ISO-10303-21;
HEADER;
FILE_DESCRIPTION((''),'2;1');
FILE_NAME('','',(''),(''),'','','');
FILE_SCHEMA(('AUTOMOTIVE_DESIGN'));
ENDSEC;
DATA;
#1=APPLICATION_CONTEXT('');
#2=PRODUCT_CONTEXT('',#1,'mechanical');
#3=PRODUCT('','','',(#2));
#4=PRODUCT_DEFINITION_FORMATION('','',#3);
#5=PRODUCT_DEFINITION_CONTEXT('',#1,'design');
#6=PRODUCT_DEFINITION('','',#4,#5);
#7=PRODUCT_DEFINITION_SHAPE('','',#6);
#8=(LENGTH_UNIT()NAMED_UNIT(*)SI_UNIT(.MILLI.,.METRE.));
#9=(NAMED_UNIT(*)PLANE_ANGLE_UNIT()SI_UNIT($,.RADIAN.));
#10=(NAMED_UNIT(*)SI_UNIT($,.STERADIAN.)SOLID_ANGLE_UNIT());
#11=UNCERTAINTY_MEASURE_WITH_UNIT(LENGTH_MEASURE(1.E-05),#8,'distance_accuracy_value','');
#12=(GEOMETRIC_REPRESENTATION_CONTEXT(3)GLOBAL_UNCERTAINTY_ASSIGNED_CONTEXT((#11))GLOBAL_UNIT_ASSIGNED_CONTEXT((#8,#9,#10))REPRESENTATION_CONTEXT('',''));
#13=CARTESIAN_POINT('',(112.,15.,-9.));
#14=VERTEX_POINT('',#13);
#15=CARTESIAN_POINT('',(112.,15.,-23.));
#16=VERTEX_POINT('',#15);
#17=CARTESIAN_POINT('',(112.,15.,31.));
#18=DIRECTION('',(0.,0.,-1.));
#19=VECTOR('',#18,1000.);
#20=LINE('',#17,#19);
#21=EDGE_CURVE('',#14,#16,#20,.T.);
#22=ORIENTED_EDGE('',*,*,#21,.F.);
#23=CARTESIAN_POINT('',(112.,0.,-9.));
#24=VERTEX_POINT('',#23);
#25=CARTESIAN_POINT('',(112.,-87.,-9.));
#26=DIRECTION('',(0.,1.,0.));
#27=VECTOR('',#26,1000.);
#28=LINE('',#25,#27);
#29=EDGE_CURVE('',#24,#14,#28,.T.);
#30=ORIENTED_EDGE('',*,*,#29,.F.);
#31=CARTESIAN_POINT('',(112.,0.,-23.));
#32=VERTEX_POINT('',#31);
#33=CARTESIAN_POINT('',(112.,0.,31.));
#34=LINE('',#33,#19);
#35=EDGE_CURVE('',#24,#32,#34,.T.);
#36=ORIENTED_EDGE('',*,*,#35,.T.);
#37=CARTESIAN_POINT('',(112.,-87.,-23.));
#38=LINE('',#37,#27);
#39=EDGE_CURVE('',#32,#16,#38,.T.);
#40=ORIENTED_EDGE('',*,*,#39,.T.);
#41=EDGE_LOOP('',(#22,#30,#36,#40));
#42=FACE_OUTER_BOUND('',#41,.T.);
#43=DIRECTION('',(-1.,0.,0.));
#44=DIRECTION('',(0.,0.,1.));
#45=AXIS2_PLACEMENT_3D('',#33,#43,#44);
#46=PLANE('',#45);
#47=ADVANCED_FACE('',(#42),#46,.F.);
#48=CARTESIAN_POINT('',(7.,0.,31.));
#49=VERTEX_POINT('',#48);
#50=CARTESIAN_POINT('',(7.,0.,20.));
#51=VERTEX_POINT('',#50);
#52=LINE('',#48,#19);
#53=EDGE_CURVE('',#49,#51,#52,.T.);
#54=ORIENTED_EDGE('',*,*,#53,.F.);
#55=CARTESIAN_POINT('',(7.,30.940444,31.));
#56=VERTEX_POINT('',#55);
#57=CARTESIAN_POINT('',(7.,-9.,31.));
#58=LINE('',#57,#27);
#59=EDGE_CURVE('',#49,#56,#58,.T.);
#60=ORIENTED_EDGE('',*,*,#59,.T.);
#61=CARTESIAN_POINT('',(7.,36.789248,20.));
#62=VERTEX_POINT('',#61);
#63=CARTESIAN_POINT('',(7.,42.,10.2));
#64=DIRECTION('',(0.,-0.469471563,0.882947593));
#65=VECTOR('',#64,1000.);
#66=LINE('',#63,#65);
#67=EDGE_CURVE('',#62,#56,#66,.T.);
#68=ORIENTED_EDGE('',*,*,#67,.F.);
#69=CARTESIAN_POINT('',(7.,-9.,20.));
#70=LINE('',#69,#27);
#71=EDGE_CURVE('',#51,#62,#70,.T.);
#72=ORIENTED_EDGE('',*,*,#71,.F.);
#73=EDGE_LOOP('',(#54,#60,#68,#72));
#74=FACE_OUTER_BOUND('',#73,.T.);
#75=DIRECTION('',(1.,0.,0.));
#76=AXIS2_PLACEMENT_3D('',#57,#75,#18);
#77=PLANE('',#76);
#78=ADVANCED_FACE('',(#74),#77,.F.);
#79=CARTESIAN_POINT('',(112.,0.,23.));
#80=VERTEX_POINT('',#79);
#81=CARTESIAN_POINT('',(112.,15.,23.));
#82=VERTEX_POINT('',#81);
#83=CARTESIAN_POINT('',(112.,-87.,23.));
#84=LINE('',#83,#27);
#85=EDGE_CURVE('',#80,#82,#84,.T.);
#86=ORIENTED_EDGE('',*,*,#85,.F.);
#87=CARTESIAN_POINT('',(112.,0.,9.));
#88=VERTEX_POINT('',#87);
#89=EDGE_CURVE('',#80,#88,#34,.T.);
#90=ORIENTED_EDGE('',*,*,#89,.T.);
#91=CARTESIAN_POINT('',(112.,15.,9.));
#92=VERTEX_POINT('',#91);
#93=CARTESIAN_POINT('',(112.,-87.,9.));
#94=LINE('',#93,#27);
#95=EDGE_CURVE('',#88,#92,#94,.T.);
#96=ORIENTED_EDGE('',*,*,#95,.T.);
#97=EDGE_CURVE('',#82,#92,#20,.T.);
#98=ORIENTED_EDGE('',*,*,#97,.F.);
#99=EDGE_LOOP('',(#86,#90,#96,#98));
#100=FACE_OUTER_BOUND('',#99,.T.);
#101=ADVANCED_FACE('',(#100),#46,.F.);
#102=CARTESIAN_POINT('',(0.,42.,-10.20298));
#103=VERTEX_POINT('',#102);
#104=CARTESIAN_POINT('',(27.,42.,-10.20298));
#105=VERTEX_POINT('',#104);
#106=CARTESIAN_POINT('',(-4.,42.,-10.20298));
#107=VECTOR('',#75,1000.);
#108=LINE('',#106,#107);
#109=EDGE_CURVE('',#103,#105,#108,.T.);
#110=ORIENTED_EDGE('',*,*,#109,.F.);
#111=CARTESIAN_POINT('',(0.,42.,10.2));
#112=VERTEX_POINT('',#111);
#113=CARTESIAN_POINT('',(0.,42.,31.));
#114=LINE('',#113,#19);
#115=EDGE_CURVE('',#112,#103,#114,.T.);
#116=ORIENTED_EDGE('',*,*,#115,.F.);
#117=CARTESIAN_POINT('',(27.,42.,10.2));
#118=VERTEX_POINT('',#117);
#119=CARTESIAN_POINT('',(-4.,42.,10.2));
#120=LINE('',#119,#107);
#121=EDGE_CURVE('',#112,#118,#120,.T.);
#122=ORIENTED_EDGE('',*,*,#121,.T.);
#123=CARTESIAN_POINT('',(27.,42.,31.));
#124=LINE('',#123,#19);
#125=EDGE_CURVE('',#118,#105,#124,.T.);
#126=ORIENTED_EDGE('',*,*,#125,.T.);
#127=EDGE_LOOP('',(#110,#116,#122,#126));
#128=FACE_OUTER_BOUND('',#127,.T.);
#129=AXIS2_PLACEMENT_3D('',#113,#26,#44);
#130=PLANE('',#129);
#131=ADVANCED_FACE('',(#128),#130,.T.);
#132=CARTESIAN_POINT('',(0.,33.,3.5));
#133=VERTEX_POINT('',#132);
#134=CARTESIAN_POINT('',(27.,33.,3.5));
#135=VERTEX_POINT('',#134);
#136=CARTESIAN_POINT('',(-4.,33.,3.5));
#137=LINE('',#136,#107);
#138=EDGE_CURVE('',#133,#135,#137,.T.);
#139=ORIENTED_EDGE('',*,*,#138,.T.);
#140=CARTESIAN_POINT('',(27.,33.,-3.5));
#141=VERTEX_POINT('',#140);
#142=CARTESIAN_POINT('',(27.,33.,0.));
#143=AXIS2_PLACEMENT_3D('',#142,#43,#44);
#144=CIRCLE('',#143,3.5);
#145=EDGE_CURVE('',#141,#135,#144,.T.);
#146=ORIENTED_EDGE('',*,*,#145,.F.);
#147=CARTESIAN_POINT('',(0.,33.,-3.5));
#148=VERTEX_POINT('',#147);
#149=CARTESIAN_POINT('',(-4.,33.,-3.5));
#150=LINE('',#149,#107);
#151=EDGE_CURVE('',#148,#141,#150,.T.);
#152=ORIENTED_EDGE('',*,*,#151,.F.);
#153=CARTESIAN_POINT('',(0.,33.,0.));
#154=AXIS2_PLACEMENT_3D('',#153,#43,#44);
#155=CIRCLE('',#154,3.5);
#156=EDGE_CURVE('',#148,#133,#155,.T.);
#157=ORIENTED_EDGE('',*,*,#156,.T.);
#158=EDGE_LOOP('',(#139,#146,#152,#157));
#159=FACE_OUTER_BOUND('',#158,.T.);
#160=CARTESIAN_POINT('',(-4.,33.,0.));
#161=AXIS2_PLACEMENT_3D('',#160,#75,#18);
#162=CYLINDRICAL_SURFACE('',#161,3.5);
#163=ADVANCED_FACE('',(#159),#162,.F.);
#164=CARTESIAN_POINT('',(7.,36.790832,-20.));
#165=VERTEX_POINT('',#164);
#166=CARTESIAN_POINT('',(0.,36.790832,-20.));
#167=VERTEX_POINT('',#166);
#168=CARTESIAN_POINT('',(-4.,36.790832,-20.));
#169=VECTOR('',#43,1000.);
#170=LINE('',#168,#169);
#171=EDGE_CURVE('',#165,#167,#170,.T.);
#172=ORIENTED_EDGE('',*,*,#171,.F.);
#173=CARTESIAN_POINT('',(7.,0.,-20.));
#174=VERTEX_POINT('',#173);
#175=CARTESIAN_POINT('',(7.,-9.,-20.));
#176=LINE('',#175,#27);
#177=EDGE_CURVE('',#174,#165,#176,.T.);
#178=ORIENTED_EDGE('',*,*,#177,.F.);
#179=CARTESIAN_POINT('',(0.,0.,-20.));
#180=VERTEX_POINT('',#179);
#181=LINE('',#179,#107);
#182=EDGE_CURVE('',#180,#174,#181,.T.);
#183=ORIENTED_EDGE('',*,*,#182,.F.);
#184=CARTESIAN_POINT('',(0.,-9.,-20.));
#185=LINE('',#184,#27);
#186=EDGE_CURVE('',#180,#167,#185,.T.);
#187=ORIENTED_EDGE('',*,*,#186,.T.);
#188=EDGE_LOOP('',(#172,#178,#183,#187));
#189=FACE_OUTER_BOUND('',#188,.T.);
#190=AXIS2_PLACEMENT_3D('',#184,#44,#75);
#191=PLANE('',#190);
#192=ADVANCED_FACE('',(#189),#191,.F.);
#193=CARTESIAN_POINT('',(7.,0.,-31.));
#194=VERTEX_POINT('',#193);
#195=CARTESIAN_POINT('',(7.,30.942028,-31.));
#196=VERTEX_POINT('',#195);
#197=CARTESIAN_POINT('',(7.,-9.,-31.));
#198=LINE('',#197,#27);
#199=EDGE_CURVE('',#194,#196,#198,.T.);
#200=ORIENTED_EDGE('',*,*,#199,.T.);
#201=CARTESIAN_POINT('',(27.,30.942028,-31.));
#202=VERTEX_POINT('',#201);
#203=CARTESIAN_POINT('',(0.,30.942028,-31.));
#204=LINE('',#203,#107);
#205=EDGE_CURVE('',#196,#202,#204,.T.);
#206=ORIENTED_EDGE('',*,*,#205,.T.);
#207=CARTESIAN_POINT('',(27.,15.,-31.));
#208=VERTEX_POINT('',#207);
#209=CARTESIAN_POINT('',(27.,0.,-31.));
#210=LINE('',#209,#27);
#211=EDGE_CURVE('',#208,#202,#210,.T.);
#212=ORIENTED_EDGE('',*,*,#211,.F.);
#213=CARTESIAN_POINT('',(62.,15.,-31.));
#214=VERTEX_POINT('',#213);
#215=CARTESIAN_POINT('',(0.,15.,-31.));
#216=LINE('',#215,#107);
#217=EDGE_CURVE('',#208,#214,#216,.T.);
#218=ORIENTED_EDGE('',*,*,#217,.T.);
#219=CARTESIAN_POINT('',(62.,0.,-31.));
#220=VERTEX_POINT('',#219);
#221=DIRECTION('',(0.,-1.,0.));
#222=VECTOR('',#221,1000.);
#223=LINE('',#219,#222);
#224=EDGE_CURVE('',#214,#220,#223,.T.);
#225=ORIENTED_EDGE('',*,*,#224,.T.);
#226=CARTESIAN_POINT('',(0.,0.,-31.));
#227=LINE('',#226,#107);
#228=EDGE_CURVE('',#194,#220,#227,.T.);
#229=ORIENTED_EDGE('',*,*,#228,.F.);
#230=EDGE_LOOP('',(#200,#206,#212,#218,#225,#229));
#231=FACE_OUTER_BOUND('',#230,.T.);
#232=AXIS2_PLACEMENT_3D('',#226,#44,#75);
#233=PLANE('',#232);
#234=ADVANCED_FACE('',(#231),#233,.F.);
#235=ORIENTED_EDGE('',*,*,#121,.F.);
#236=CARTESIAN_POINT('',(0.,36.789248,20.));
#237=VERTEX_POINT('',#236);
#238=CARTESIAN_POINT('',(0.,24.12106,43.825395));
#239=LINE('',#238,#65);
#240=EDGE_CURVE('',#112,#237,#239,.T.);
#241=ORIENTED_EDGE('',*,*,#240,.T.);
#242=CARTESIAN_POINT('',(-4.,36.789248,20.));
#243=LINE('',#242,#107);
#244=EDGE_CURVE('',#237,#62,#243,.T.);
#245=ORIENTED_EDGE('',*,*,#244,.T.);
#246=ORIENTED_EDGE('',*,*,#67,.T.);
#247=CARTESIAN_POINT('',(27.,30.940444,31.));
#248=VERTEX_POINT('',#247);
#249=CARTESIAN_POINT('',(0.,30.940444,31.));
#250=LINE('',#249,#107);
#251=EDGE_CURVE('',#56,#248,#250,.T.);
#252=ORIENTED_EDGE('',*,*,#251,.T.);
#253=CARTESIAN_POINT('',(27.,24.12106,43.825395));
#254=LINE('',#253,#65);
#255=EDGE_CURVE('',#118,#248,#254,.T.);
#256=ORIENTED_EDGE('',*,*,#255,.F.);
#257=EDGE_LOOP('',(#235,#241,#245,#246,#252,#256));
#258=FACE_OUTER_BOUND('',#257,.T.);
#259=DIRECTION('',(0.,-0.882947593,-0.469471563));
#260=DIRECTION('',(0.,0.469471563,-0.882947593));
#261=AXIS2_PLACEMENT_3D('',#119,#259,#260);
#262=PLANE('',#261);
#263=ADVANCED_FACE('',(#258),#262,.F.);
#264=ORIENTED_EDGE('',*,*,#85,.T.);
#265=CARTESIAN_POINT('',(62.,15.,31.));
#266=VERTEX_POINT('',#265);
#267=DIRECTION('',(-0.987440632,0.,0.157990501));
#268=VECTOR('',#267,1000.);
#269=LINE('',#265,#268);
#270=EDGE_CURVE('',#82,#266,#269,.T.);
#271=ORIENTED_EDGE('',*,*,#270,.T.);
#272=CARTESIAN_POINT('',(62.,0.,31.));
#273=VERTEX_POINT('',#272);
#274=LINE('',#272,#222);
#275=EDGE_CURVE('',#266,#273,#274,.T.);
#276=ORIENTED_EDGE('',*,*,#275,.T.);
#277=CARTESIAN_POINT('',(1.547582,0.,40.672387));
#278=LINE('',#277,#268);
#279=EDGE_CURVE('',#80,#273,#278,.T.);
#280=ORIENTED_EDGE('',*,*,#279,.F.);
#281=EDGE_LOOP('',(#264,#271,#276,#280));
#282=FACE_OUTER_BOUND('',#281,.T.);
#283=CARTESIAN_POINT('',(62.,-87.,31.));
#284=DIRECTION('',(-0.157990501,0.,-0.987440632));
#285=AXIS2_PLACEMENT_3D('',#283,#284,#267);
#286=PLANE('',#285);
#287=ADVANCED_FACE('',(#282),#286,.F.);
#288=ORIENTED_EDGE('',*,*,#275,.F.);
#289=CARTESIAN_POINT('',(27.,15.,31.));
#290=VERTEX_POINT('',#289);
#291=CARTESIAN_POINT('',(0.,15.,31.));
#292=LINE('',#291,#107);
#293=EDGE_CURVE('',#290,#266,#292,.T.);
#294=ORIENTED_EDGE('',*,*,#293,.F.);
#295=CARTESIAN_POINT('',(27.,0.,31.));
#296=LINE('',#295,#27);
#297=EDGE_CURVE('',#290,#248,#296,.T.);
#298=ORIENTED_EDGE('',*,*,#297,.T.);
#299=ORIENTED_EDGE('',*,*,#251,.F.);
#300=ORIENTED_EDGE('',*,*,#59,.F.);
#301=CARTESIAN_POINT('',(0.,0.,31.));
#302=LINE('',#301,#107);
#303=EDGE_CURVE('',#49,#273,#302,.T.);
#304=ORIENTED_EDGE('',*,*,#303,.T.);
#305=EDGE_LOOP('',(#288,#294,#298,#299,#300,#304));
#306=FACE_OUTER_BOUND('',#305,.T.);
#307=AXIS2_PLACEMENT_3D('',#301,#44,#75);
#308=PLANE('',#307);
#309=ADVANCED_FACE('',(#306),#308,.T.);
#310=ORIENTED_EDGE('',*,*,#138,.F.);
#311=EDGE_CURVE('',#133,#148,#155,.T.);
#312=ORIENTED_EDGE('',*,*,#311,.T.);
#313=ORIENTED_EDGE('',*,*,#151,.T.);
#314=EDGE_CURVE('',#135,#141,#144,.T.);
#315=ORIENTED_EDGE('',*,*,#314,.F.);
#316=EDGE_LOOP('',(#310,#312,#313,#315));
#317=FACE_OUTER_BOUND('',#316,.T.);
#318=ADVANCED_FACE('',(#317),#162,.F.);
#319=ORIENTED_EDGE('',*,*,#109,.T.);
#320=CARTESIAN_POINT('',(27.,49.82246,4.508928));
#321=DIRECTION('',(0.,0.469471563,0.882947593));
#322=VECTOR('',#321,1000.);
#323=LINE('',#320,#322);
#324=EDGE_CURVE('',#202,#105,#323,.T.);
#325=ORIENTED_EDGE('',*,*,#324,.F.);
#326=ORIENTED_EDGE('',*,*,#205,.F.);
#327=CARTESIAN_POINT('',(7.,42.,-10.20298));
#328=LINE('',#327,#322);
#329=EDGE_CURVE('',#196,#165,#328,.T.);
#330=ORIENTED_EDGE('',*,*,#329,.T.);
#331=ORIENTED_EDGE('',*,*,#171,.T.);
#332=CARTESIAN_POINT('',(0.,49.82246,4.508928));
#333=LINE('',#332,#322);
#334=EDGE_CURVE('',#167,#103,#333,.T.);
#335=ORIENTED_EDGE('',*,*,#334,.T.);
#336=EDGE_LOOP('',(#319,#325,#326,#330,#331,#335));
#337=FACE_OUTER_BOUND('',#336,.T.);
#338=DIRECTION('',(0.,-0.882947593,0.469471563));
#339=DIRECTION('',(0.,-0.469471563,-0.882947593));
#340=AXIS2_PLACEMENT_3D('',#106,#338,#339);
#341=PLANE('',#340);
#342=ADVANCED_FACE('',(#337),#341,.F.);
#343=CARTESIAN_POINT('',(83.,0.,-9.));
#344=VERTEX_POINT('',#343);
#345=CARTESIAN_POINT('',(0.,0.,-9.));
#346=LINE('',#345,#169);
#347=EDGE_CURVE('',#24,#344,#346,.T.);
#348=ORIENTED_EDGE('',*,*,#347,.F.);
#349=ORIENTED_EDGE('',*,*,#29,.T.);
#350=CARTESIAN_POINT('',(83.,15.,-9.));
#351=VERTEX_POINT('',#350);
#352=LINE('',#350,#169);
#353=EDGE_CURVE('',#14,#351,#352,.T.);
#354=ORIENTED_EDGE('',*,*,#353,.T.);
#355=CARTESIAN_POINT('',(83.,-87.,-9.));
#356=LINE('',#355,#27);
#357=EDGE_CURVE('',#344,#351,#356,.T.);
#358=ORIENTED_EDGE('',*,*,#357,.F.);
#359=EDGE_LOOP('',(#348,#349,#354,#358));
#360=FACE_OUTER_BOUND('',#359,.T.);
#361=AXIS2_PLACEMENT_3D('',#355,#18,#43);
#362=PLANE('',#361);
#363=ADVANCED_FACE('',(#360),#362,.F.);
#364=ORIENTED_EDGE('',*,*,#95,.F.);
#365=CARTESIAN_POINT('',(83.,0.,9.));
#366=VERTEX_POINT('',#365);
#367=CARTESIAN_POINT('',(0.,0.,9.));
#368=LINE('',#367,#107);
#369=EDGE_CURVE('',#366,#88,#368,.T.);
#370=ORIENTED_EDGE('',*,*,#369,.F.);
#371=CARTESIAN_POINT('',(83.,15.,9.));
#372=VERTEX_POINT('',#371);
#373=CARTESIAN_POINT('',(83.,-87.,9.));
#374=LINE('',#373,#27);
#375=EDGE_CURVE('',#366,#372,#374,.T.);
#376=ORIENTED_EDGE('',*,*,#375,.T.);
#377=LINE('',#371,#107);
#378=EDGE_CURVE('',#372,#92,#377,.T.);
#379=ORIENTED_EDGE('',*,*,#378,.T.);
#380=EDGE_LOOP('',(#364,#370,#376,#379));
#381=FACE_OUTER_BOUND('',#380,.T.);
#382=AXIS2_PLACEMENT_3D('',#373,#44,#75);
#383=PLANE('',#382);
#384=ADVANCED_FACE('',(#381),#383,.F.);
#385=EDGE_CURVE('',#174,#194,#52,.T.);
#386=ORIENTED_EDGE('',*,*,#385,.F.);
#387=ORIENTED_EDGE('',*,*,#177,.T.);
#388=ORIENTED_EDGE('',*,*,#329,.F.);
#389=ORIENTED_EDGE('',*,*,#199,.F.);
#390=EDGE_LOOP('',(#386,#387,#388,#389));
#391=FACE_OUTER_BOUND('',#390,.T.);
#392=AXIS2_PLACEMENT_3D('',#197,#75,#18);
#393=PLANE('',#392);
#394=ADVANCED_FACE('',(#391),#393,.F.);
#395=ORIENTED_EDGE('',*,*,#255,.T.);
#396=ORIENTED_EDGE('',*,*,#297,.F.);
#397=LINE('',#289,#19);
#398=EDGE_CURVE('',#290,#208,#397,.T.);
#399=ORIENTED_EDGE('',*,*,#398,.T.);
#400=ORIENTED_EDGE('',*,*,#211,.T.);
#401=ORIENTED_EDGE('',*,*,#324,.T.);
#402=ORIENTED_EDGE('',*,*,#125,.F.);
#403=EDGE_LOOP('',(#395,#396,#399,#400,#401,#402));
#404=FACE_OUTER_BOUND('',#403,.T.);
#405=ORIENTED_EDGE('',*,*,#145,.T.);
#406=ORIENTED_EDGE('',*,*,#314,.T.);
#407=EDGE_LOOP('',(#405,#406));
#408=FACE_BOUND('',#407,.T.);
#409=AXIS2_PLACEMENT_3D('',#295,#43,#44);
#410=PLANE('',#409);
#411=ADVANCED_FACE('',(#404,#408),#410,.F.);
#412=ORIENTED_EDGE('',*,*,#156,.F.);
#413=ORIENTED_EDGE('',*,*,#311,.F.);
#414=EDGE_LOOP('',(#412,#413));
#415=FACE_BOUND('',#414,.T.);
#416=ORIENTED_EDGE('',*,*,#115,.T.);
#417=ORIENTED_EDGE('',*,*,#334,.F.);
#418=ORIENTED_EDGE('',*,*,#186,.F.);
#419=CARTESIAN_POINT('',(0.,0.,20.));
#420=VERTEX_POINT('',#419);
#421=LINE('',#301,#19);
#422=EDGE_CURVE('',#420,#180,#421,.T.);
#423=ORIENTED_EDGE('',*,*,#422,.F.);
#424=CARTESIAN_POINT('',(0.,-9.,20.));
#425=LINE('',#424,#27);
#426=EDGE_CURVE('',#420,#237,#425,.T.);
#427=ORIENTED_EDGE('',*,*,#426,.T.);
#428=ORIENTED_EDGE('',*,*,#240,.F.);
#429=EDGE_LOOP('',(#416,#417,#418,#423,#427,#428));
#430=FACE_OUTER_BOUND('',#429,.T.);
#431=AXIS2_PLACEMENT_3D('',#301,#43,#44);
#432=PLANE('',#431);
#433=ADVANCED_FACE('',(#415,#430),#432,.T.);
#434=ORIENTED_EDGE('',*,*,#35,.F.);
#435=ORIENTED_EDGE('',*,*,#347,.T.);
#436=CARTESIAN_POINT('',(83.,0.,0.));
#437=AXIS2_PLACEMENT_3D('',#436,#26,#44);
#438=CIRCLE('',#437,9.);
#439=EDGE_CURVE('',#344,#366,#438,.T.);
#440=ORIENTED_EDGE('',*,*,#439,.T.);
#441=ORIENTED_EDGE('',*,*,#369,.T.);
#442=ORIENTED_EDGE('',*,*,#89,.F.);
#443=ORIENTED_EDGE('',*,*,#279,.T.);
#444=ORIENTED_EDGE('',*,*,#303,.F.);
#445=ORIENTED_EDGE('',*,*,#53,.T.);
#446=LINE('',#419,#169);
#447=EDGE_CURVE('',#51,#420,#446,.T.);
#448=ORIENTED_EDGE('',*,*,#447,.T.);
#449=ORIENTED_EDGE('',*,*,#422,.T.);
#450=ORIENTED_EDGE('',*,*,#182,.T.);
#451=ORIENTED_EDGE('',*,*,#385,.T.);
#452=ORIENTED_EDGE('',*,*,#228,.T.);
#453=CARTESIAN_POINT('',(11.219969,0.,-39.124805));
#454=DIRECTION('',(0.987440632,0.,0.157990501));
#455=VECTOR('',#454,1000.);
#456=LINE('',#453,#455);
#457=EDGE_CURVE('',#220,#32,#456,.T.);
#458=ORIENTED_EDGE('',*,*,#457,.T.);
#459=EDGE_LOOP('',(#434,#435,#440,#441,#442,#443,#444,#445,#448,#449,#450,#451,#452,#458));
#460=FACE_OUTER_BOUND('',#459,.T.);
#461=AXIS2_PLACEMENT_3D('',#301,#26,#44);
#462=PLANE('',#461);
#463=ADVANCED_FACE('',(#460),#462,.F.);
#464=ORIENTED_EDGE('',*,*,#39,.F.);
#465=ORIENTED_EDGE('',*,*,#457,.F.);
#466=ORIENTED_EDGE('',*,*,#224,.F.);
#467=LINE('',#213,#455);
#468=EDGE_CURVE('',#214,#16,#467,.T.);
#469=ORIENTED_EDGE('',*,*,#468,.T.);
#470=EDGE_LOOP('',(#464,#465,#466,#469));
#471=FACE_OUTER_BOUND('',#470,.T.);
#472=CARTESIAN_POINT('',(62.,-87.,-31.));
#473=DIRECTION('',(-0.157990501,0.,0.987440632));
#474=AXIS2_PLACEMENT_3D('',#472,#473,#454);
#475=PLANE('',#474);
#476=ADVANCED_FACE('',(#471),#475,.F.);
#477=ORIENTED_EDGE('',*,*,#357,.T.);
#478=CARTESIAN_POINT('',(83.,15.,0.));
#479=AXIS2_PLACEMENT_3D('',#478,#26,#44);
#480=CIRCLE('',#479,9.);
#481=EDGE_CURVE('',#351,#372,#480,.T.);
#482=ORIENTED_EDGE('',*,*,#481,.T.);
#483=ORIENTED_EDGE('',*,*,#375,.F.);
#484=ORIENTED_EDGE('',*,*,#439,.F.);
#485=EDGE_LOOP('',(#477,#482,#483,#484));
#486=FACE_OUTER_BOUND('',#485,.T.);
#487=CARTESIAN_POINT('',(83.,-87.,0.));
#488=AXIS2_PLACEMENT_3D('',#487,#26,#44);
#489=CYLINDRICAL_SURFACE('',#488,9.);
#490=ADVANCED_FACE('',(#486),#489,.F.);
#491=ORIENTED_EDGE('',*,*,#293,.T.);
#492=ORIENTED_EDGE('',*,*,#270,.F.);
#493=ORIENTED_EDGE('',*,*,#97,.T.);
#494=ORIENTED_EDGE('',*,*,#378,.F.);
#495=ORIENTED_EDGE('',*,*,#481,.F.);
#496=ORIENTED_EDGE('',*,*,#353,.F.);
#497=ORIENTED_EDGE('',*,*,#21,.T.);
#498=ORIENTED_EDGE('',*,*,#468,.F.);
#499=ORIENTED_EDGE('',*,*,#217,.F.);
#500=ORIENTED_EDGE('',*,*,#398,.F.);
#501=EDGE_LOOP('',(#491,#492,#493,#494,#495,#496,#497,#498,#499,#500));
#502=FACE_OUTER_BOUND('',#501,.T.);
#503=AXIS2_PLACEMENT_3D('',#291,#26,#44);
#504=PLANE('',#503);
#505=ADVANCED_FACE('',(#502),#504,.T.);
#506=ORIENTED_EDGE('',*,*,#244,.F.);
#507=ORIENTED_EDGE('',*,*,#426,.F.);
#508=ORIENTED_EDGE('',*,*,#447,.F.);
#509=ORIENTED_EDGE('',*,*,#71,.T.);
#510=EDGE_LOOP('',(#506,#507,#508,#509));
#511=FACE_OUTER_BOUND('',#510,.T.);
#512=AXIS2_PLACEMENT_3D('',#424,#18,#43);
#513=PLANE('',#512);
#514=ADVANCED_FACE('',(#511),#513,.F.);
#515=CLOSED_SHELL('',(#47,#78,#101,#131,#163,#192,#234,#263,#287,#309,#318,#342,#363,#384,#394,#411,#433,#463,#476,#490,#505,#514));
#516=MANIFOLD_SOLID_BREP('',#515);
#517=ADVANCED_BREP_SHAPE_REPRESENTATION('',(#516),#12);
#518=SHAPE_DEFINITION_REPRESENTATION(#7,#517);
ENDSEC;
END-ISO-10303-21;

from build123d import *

# Parameters (mm, degrees)
BRACKET_BODY_DEPTH     = 31
HEAD_CHAMFER_SKETCH_R  = 3.5
HEAD_CHAMFER_CUT_DEPTH = 31
HEAD_NOTCH_SKETCH_W    = 7
HEAD_NOTCH_SKETCH_H    = 11
HEAD_NOTCH_CUT_DEPTH   = 51
FORKED_SLOT_CUT_DEPTH  = 102


with BuildPart() as part:
    # Bracket Profile Sketch → Bracket Body (new, symmetric)
    with BuildSketch(Plane.XY):
        Polygon((0, 15), (0, 0), (27, 0), (112, 0), (112, 15), (27, 15), (27, 42), (0, 42), align=None)
    extrude(amount=BRACKET_BODY_DEPTH, both=True)

    # Head Chamfer Sketch → Head Chamfer Cut (cut, symmetric)
    with BuildSketch(Plane(origin=(27, 0, 0), x_dir=(0, 0, -1), z_dir=(1, 0, 0))):
        with Locations(Location((0, 33, 0), (0, 0, 180))):
            Circle(HEAD_CHAMFER_SKETCH_R)
        Polygon((10.202979839, 42), (31, 30.94202823), (31, 54.961145536), (-31, 54.961145536), (-31, 30.940443821), (-10.2, 42), align=None)
    extrude(amount=HEAD_CHAMFER_CUT_DEPTH, both=True, mode=Mode.SUBTRACT)

    # Head Notch Sketch → Head Notch Cut (cut, symmetric)
    with BuildSketch(Plane(origin=(0, 42, 0), x_dir=(1, 0, 0), z_dir=(0, 1, 0))):
        with Locations((3.5, 25.5)):
            Rectangle(HEAD_NOTCH_SKETCH_W, HEAD_NOTCH_SKETCH_H)
        with Locations((3.5, -25.5)):
            Rectangle(HEAD_NOTCH_SKETCH_W, HEAD_NOTCH_SKETCH_H)
    extrude(amount=HEAD_NOTCH_CUT_DEPTH, both=True, mode=Mode.SUBTRACT)

    # Forked Slot Sketch → Forked Slot Cut (cut)
    with BuildSketch(Plane(origin=(0, 15, 0), x_dir=(1, 0, 0), z_dir=(0, 1, 0))):
        Polygon((62, -31), (112, -23), (112, -31), align=None)
        Polygon((62, 31), (112, 23), (112, 31), align=None)
        with BuildLine():
            Line((83, 9), (112, 9))
            Line((112, 9), (112, -9))
            Line((112, -9), (83, -9))
            ThreePointArc((83, -9), (74, 0), (83, 9))
        make_face()
    extrude(amount=-FORKED_SLOT_CUT_DEPTH, mode=Mode.SUBTRACT)


solid = part.part
